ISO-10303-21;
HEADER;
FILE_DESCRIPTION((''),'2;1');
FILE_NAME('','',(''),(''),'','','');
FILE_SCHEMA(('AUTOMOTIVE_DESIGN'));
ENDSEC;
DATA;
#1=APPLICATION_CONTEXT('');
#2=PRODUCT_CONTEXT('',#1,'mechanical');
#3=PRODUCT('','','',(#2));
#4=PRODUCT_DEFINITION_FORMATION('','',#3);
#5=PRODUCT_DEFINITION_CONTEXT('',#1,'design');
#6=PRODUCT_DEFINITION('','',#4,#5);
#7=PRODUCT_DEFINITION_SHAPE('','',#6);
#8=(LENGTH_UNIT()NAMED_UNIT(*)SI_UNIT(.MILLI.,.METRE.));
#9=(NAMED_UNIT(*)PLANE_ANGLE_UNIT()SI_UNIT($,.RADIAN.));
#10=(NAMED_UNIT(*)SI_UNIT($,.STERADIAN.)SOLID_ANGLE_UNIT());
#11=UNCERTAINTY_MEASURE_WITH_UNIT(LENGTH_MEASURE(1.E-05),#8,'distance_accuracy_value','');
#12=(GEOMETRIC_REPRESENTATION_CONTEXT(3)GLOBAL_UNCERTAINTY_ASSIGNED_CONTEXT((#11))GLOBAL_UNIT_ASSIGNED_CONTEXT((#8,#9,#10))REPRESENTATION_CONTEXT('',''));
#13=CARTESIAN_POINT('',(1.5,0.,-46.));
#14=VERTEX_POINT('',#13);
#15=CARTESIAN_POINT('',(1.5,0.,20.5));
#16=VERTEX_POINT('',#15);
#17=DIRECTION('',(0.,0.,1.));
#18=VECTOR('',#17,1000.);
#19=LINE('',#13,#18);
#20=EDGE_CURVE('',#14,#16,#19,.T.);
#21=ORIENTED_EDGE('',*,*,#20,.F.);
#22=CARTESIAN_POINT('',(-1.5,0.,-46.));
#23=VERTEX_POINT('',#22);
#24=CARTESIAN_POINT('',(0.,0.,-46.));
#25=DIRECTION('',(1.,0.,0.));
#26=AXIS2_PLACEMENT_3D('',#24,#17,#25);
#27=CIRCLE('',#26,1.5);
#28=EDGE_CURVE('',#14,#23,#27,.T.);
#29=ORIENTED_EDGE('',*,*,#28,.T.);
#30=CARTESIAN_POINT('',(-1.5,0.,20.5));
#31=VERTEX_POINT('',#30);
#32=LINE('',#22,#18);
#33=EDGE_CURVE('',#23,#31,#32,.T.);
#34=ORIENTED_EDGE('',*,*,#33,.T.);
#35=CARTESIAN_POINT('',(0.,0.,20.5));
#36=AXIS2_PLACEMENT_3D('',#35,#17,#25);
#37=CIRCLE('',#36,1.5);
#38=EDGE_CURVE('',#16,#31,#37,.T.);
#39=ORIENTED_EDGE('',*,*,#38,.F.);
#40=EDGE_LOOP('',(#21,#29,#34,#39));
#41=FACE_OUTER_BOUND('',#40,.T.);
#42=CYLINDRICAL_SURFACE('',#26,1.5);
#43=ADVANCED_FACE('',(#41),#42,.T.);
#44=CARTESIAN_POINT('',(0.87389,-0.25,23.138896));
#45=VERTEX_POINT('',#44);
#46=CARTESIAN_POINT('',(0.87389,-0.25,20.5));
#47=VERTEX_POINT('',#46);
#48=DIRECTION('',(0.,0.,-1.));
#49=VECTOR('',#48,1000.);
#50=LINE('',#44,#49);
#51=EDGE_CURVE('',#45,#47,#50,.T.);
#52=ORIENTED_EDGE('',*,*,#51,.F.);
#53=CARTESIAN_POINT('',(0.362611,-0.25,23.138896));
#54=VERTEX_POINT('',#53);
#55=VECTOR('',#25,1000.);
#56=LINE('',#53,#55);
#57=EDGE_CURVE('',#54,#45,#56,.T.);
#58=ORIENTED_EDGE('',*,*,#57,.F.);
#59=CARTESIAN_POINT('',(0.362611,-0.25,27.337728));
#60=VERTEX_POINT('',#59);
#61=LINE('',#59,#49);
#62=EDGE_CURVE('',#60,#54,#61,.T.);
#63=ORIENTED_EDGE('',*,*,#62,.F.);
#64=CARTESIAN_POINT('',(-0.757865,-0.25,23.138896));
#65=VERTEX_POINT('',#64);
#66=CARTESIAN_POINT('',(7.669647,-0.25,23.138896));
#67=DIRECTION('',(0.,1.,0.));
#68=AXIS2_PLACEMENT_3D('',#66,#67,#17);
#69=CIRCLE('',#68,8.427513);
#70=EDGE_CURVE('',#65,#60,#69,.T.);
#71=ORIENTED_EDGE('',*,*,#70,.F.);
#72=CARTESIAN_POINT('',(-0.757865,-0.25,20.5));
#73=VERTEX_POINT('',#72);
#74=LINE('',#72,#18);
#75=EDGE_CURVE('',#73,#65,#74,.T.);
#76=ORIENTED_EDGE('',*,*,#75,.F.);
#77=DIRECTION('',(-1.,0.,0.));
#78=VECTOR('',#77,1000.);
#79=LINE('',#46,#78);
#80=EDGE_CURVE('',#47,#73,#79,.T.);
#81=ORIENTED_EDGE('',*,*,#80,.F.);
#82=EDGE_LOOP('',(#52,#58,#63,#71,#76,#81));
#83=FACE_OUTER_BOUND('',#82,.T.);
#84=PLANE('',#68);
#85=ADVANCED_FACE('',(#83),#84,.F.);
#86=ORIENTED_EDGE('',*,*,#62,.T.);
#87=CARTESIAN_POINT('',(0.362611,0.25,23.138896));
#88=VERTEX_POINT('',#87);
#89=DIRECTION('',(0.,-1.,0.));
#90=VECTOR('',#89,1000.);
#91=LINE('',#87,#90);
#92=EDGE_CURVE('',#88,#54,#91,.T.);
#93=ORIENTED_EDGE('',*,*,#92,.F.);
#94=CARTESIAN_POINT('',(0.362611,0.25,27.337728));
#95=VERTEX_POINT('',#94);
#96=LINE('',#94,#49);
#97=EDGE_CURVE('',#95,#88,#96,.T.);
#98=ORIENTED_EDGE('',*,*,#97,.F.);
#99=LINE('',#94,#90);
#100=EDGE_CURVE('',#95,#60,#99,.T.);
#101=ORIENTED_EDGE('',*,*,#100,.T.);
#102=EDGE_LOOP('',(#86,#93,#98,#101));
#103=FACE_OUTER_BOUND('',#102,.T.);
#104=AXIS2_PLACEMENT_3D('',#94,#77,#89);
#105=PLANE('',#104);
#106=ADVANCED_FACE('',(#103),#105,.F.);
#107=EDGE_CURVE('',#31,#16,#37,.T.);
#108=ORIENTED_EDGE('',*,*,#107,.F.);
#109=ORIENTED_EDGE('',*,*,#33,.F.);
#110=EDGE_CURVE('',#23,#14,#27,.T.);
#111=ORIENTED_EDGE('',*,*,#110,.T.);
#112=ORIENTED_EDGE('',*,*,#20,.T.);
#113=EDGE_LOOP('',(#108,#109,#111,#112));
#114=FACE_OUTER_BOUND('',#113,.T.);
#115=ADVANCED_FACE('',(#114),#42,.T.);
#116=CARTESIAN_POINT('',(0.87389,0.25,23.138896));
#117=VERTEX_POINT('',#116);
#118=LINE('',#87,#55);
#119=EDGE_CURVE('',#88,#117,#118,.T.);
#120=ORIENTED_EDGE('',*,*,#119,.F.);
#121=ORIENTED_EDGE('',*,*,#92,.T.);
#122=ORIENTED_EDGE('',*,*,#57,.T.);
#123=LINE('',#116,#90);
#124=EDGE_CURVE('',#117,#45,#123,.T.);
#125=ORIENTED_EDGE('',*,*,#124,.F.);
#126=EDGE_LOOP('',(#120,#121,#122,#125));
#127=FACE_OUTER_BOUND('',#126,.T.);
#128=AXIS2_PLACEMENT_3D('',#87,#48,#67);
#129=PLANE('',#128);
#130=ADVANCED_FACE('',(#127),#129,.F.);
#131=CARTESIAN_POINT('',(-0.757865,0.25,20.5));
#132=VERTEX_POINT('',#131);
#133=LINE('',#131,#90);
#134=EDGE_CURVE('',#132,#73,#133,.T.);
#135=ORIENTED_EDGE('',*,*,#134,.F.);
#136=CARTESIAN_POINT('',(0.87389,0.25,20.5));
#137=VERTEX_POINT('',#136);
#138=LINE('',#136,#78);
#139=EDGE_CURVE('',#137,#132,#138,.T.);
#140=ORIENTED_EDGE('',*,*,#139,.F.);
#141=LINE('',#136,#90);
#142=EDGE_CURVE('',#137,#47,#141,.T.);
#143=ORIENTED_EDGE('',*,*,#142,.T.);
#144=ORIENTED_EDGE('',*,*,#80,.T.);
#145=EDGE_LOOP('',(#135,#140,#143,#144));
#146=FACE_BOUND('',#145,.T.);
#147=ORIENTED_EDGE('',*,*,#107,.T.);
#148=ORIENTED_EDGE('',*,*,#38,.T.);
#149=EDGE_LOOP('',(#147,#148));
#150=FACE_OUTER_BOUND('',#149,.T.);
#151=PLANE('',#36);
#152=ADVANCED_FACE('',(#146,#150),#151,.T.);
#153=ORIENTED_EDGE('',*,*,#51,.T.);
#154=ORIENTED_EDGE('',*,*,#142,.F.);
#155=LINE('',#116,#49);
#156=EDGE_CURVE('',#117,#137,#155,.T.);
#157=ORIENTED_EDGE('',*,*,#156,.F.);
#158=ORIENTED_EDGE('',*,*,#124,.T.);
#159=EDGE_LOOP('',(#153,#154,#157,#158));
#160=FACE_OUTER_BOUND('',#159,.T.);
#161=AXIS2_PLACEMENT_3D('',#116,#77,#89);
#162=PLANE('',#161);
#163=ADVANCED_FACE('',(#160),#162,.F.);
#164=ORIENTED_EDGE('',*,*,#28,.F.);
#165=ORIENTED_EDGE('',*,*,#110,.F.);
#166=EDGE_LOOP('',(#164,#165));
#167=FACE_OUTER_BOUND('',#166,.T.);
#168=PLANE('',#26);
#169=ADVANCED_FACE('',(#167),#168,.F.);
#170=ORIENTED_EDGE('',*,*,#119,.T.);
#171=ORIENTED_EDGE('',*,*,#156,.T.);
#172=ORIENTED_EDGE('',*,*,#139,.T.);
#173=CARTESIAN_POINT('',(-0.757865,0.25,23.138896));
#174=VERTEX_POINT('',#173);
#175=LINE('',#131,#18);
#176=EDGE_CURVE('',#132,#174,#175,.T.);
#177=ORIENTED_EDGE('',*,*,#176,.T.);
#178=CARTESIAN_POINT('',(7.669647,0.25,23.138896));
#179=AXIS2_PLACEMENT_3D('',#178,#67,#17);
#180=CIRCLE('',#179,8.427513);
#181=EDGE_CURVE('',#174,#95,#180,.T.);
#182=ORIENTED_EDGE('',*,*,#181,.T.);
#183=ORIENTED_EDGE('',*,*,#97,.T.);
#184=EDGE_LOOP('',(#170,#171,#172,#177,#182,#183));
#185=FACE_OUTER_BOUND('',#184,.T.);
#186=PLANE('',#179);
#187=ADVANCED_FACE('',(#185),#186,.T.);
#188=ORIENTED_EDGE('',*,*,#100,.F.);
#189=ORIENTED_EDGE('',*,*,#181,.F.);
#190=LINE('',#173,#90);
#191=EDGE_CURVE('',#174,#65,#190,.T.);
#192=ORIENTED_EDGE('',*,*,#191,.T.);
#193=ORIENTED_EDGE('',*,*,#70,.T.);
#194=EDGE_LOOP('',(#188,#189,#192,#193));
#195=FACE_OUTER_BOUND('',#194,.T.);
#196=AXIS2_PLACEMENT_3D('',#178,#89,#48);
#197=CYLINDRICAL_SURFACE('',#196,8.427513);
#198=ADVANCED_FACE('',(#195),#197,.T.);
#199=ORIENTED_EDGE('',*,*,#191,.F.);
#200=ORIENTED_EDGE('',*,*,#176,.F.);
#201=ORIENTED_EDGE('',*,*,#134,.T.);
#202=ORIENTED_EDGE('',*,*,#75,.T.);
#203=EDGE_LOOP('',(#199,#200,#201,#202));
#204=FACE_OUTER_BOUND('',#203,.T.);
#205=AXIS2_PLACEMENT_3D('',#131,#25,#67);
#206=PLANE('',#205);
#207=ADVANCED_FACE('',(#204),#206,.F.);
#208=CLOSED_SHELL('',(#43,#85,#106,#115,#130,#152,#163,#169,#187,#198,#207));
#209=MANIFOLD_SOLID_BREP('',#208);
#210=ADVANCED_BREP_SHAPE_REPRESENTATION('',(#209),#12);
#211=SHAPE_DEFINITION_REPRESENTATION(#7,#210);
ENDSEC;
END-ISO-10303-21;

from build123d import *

# Parameters (mm, degrees)
BOSS_EXTRUDE1_DEPTH      = 20
BOSS_EXTRUDE1_DEPTH_BACK = 46
SKETCH1_R                = 1.5
SKETCH2_R                = 1.5
BOSS_EXTRUDE2_DEPTH      = 0.5
BOSS_EXTRUDE3_DEPTH      = 0.25


with BuildPart() as part:
    # Sketch1 → Boss-Extrude1 (new, two sides: drawn at the far end of the back side and taken through both)
    with BuildSketch(Plane.XY.offset(-BOSS_EXTRUDE1_DEPTH_BACK)):
        Circle(SKETCH1_R)
    extrude(amount=BOSS_EXTRUDE1_DEPTH + BOSS_EXTRUDE1_DEPTH_BACK)

    # Sketch2 → Boss-Extrude2 (add)
    with BuildSketch(Plane.XY.offset(20)):
        Circle(SKETCH2_R)
    extrude(amount=BOSS_EXTRUDE2_DEPTH)

    # Sketch3 → Boss-Extrude3 (add, symmetric)
    with BuildSketch(Plane(origin=(0, 0, 0), x_dir=(1, 0, 0), z_dir=(0, 1, 0))):
        with BuildLine():
            Line((0.873889529, -20.5), (-0.757865329, -20.5))
            Line((-0.757865329, -20.5), (-0.757865329, -23.138895886))
            ThreePointArc((-0.757865329, -23.138895886), (-0.472929345, -25.311777544), (0.362611115, -27.337728025))
            Line((0.362611115, -27.337728025), (0.362611115, -23.138895886))
            Line((0.362611115, -23.138895886), (0.873889529, -23.138895886))
            Line((0.873889529, -23.138895886), (0.873889529, -20.5))
        make_face()
    extrude(amount=BOSS_EXTRUDE3_DEPTH, both=True)


solid = part.part
